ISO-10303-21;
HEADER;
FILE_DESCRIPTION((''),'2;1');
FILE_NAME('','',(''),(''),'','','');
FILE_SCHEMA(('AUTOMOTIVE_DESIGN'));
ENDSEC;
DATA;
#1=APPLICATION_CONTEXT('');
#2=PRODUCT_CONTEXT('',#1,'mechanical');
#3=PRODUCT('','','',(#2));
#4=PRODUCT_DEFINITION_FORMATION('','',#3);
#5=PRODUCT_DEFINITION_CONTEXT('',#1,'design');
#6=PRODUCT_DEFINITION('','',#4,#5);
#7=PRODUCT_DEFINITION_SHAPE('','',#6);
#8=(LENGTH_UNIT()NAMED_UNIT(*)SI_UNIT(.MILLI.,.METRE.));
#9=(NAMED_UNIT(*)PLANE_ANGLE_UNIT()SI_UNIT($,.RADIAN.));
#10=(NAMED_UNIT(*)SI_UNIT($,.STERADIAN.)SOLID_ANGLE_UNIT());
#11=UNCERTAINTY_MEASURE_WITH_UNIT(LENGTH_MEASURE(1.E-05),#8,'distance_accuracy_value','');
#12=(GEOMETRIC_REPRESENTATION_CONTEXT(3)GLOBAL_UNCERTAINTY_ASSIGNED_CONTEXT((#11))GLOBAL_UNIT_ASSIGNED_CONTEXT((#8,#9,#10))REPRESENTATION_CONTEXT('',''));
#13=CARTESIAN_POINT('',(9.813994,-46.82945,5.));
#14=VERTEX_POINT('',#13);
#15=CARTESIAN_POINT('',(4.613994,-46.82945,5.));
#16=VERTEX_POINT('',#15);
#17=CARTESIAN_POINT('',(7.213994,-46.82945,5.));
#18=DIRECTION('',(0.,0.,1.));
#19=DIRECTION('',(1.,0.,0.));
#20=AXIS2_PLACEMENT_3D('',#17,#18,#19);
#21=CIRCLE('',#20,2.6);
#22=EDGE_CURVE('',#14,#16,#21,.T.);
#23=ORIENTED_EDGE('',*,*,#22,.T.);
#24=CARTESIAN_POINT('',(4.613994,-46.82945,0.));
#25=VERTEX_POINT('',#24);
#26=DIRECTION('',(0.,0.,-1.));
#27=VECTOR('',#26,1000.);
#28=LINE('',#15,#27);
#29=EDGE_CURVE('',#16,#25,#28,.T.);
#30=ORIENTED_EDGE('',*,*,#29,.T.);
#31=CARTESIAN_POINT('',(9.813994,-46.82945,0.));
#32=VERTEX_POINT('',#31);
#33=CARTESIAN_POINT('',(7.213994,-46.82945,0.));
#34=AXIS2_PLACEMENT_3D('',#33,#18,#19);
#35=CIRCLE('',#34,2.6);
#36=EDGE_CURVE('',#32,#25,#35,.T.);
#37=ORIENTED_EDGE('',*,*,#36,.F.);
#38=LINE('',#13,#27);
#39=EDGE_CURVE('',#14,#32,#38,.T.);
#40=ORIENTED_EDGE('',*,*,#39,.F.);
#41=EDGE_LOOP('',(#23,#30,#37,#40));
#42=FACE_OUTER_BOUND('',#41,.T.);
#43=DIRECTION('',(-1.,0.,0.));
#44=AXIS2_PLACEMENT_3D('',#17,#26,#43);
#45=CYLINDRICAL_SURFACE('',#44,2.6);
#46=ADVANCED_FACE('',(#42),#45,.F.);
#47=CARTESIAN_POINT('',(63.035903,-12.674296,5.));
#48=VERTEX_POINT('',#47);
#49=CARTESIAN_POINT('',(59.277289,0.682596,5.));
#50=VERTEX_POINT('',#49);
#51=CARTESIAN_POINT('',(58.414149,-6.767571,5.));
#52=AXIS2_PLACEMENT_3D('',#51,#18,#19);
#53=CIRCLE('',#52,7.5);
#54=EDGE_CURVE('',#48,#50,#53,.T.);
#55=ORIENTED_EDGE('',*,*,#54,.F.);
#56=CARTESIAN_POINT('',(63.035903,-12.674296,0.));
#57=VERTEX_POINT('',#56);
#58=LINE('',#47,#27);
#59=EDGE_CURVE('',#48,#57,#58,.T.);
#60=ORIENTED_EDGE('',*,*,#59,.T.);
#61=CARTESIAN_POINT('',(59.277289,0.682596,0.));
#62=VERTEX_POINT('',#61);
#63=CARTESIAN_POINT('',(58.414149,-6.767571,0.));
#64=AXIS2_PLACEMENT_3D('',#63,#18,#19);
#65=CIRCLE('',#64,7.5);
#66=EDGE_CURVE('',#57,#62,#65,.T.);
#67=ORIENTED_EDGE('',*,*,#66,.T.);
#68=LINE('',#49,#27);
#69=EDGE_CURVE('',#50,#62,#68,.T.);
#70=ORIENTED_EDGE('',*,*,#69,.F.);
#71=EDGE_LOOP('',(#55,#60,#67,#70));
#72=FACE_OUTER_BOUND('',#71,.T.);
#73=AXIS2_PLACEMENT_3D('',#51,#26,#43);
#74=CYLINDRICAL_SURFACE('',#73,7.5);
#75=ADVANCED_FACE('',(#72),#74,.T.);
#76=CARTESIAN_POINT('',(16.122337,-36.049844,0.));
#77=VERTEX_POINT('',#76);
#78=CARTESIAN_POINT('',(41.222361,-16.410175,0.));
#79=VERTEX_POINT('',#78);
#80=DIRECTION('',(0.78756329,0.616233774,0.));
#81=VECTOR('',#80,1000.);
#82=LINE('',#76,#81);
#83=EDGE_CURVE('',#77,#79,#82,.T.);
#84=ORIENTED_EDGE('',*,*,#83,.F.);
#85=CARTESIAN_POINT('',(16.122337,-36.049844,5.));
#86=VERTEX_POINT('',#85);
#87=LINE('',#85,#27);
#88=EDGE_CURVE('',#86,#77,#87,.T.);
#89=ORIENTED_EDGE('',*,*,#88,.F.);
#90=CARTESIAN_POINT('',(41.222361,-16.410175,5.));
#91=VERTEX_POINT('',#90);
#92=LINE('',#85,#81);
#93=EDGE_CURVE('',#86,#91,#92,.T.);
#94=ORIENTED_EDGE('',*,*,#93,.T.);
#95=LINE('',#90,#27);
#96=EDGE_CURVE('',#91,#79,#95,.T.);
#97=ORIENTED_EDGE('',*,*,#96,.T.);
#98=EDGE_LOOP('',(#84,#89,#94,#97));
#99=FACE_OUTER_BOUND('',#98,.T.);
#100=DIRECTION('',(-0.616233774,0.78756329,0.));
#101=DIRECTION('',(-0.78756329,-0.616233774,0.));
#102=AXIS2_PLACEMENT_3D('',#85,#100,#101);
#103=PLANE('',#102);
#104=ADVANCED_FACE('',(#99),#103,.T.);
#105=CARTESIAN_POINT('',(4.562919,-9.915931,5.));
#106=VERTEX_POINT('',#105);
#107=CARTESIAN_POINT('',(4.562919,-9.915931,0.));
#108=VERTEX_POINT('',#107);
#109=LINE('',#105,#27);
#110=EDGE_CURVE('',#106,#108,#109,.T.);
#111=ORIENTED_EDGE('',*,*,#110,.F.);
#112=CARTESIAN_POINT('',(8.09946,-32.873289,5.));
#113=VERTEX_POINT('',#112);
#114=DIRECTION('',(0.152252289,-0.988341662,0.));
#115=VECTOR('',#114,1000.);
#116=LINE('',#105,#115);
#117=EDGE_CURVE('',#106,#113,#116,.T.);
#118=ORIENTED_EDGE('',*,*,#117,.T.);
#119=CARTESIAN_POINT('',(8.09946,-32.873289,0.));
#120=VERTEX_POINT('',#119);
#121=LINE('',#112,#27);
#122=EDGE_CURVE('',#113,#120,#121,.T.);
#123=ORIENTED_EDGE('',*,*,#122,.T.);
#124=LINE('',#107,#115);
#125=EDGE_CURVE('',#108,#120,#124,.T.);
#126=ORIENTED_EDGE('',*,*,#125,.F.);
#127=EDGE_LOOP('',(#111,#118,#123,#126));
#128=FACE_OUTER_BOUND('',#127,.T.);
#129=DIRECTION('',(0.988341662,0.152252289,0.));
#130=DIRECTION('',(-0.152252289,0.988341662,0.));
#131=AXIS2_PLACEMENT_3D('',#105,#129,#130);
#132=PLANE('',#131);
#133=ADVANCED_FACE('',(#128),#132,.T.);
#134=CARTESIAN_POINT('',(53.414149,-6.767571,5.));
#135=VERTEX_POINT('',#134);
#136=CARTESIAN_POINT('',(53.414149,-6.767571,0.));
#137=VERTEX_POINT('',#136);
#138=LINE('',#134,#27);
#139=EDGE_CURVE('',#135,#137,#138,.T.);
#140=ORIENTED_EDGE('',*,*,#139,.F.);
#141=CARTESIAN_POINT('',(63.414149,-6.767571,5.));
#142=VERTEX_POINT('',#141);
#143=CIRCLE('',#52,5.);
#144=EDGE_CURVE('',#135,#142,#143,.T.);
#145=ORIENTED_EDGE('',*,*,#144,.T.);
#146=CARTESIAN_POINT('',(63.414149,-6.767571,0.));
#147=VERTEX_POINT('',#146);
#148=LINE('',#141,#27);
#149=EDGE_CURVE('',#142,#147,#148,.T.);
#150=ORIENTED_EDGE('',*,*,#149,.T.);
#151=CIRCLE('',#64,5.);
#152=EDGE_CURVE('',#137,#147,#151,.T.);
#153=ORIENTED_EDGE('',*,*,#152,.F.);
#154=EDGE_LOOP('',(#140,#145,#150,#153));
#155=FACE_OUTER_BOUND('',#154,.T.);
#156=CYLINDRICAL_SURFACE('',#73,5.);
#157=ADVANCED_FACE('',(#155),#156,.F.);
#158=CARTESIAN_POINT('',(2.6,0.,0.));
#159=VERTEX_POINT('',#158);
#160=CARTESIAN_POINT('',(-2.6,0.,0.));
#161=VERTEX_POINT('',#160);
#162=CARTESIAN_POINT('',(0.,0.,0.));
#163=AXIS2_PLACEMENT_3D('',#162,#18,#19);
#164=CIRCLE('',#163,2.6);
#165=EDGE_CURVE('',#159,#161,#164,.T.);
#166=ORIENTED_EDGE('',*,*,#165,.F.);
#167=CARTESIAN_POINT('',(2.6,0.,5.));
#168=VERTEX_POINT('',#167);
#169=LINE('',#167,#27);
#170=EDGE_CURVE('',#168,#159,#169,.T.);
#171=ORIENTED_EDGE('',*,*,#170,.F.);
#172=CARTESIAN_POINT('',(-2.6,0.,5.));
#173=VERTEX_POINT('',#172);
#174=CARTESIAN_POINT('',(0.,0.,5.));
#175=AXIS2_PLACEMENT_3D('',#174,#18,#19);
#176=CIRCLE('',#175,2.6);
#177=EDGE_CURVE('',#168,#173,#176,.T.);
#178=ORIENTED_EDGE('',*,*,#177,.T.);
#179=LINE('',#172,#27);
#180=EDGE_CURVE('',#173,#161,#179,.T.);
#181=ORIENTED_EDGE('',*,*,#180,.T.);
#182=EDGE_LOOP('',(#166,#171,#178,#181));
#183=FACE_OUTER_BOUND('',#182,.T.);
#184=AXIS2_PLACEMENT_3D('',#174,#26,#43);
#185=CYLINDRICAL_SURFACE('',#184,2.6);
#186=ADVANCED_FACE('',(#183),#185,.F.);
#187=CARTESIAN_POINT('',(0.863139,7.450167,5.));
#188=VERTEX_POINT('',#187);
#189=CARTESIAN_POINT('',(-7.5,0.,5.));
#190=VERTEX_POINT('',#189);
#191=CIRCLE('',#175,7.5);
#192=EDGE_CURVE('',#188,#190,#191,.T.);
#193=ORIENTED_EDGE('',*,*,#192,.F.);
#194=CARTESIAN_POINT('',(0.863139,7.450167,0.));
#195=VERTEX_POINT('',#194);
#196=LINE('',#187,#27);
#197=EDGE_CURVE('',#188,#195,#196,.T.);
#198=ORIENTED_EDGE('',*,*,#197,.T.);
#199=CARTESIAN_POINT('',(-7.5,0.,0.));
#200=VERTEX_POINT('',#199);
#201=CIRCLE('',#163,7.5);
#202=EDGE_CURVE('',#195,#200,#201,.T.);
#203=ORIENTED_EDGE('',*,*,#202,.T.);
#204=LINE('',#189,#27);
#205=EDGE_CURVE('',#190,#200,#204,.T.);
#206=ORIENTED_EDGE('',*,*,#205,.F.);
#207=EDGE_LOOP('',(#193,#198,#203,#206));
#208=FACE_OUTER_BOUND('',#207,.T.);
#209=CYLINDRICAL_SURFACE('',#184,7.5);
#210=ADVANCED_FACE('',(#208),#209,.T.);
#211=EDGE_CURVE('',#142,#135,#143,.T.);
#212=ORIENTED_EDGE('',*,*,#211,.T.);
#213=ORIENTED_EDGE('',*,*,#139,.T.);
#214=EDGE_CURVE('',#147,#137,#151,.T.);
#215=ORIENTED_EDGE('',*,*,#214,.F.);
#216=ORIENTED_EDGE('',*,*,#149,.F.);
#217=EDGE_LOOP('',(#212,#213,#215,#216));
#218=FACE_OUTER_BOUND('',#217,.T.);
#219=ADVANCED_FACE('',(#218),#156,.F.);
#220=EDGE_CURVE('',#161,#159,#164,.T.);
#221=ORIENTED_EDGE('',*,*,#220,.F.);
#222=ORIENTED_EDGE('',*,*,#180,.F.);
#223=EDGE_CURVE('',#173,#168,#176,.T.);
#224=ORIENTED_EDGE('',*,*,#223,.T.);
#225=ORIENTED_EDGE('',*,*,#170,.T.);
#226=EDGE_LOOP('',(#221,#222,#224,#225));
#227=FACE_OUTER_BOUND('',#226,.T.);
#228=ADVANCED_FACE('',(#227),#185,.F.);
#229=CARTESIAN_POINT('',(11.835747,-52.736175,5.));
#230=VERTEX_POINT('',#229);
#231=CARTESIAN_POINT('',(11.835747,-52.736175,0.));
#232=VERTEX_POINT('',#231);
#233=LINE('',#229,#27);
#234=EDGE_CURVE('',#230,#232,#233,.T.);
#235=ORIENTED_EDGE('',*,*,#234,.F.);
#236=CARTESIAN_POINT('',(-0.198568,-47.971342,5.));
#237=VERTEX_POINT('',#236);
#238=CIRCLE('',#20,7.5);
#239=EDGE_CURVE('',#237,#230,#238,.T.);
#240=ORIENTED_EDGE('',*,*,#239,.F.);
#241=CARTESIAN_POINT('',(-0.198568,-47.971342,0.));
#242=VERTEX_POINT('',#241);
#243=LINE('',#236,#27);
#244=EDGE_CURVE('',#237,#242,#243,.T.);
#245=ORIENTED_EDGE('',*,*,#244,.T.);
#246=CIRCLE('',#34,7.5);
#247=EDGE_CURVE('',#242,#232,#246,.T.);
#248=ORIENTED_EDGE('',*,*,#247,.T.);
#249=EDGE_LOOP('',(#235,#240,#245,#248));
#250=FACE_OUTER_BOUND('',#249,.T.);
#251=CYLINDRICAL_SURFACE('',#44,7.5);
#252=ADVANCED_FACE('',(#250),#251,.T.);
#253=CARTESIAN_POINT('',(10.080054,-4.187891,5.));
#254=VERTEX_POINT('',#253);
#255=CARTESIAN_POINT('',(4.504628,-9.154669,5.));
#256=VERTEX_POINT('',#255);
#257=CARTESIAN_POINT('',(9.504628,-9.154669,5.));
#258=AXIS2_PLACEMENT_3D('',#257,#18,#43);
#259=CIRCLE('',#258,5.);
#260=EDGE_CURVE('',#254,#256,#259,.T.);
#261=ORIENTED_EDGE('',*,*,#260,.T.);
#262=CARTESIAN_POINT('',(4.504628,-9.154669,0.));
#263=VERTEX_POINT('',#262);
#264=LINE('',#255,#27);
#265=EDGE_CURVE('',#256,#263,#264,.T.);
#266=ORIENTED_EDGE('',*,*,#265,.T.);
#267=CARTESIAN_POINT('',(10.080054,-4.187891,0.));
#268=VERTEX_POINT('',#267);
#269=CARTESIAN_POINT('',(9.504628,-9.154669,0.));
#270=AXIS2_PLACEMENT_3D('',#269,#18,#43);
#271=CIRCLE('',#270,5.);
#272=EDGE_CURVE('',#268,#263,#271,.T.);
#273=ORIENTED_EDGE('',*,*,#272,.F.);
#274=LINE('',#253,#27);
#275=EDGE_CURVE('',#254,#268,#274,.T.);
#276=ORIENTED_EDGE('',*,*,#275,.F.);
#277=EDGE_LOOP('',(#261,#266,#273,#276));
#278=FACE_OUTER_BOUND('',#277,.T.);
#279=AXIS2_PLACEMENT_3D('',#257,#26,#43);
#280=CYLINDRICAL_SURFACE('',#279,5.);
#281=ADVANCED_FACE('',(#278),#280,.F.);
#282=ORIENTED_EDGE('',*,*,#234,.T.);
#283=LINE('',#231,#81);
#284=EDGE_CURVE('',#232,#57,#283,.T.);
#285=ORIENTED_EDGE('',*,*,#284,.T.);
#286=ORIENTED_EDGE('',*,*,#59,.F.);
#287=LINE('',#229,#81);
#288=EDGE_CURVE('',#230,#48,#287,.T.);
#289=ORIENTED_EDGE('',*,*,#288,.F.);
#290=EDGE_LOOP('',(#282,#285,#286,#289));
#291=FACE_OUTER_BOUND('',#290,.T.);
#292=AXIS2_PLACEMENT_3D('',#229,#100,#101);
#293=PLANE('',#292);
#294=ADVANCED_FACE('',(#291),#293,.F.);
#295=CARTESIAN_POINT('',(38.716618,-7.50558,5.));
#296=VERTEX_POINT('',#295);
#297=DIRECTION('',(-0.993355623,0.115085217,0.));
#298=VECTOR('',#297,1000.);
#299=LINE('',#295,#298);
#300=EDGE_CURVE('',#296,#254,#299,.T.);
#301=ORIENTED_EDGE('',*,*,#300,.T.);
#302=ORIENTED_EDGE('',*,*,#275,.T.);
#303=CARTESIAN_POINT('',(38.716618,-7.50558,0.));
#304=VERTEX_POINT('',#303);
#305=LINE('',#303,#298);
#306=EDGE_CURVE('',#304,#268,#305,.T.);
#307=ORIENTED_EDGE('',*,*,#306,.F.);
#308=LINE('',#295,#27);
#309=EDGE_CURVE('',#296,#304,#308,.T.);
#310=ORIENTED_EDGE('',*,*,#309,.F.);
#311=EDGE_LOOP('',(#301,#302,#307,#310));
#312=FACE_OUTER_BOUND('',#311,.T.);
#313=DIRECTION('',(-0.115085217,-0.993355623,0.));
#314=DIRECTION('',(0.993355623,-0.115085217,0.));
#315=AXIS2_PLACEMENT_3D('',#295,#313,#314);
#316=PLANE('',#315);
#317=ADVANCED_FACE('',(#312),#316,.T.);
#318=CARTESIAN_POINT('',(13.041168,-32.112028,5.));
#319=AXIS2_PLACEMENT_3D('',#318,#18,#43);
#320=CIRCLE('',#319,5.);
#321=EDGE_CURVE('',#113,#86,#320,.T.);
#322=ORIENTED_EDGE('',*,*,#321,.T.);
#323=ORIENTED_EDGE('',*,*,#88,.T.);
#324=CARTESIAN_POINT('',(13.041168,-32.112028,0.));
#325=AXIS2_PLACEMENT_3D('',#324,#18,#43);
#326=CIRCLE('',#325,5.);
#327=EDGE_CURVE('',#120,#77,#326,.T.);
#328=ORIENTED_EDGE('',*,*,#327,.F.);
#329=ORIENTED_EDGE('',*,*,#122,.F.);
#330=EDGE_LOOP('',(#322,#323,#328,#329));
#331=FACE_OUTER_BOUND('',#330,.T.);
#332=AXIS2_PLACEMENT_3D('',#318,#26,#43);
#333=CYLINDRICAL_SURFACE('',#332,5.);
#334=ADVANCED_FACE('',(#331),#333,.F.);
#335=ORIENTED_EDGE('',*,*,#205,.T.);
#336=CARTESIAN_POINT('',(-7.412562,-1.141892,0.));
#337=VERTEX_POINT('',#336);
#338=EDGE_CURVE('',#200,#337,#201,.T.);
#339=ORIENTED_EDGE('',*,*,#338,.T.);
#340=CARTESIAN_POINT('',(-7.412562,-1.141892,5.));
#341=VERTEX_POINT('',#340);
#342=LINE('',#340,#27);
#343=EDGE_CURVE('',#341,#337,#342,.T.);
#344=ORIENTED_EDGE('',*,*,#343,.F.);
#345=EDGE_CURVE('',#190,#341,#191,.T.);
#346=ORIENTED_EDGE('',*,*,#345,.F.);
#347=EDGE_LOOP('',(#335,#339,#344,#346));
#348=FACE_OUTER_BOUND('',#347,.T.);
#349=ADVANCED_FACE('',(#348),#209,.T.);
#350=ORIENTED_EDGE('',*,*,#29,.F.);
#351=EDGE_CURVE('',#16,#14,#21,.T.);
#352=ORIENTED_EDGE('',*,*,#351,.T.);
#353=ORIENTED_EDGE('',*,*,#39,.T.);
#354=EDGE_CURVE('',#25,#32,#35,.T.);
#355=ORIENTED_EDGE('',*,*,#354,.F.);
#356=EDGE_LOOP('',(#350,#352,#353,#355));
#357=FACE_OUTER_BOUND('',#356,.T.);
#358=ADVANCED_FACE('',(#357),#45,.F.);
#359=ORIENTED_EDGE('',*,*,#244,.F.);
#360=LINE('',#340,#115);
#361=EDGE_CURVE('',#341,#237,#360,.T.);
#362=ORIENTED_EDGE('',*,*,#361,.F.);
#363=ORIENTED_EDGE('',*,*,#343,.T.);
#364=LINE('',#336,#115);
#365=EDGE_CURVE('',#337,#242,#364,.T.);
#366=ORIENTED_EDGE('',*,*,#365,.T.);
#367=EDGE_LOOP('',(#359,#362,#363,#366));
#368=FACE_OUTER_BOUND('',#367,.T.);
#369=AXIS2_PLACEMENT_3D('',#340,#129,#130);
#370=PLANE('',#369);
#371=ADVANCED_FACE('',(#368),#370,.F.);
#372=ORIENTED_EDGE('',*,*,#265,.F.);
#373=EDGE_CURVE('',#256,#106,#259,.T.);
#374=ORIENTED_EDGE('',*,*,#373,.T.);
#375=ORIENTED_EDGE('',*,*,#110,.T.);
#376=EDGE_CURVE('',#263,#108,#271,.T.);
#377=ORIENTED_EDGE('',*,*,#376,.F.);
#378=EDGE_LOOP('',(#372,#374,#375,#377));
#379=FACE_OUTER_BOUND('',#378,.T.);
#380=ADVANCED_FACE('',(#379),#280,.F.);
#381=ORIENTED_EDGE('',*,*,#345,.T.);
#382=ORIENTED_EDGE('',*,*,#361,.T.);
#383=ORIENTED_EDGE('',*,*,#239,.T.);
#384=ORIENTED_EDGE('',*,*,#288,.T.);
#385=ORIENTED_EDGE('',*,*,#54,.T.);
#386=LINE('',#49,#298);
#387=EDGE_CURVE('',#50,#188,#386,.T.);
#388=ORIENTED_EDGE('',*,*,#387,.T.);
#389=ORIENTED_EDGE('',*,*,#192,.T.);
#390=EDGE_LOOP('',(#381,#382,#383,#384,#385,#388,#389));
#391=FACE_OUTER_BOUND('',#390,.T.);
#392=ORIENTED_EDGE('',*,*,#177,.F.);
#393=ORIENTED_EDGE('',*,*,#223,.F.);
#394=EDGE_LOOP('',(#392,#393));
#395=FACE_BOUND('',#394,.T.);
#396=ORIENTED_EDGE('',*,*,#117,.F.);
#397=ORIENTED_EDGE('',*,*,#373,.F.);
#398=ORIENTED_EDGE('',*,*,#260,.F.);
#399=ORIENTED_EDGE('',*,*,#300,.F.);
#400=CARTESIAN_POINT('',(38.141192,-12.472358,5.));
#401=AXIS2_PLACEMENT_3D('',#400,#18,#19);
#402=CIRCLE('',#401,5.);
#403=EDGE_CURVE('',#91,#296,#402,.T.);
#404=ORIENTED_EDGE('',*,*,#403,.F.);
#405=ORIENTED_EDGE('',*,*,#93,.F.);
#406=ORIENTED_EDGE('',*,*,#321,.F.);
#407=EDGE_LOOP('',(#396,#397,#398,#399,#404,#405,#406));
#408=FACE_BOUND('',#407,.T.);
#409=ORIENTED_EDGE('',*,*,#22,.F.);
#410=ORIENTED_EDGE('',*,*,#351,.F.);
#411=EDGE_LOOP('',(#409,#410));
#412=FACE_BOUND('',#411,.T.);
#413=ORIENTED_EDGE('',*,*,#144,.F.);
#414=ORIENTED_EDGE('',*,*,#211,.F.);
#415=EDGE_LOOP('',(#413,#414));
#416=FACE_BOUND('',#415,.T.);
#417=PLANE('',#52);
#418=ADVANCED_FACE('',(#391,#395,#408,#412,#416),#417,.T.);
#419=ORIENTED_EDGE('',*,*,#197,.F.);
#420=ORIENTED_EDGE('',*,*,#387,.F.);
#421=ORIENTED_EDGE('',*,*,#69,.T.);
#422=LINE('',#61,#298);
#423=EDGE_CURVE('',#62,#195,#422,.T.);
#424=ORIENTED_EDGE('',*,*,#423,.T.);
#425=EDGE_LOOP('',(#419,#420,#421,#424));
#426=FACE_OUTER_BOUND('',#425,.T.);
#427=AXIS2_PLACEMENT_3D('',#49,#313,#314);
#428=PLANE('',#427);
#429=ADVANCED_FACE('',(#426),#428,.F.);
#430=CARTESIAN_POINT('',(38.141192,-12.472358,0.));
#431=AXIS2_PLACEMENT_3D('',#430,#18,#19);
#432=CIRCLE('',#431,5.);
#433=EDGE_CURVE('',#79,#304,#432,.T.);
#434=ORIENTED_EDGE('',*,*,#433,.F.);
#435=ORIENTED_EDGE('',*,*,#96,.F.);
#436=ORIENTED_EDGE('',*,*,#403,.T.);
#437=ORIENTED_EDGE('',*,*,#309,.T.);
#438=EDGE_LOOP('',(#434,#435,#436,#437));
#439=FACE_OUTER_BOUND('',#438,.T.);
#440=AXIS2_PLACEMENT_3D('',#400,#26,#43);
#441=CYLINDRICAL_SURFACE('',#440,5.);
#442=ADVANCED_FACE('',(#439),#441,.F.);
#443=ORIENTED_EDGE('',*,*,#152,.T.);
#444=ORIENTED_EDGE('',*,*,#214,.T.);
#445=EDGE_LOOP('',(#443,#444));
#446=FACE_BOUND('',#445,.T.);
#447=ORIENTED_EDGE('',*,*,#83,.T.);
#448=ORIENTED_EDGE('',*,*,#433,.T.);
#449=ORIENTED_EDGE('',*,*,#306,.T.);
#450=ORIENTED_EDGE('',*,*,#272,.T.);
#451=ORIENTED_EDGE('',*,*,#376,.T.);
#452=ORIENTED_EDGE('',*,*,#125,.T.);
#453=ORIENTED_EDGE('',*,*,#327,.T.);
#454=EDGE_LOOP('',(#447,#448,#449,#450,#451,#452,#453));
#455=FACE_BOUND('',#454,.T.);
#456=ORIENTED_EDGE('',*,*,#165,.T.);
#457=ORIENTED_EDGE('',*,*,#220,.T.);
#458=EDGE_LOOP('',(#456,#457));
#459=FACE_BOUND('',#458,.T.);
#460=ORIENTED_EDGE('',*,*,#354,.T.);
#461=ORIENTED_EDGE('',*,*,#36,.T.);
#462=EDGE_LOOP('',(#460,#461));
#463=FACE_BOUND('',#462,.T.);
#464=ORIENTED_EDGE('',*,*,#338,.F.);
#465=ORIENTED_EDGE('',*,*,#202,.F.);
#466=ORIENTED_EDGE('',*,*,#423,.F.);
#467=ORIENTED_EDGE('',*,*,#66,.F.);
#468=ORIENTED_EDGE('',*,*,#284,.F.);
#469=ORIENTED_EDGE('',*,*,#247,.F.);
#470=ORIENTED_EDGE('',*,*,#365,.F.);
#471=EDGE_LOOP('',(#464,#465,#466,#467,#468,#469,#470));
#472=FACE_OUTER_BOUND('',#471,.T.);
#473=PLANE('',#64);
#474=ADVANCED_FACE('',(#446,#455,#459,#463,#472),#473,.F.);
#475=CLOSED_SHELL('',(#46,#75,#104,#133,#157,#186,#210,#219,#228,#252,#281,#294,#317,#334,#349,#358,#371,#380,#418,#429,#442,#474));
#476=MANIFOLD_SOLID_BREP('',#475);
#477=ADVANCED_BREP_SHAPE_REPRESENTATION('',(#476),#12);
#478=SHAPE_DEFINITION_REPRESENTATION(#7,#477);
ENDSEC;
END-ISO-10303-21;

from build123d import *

# Parameters (mm, degrees)
SKETCH1_R           = 5
SKETCH1_R_2         = 2.6
BOSS_EXTRUDE1_DEPTH = 5


with BuildPart() as part:
    # Sketch1 → Boss-Extrude1 (new body)
    with BuildSketch(Plane.XY):
        with BuildLine():
            Line((-7.412562463, -1.141892169), (-0.198568318, -47.971342146))
            ThreePointArc((-0.198568318, -47.971342146), (4.453004984, -53.802751838), (11.835747448, -52.736174654))
            Line((11.835747448, -52.736174654), (63.035902792, -12.674296032))
            ThreePointArc((63.035902792, -12.674296032), (65.633751361, -4.735983598), (59.277288615, 0.682595814))
            Line((59.277288615, 0.682595814), (0.863139126, 7.450167169))
            ThreePointArc((0.863139126, 7.450167169), (-5.401815198, 5.202921542), (-7.412562463, -1.141892169))
        make_face()
        with Locations((58.414149489, -6.767571355)):
            Circle(SKETCH1_R, mode=Mode.SUBTRACT)
        with Locations((7.213994146, -46.829449977)):
            Circle(SKETCH1_R_2, mode=Mode.SUBTRACT)
        Circle(SKETCH1_R_2, mode=Mode.SUBTRACT)
        with BuildLine():
            Line((38.716618419, -7.505580332), (10.080053588, -4.187891081))
            ThreePointArc((10.080053588, -4.187891081), (5.903417372, -5.686054833), (4.562919195, -9.91593064))
            Line((4.562919195, -9.91593064), (8.099459791, -32.873289294))
            ThreePointArc((8.099459791, -32.873289294), (11.200508659, -36.760895756), (16.122336968, -36.049844299))
            Line((16.122336968, -36.049844299), (41.222361204, -16.410174896))
            ThreePointArc((41.222361204, -16.410174896), (42.95426025, -11.117966607), (38.716618419, -7.505580332))
        make_face(mode=Mode.SUBTRACT)
    extrude(amount=BOSS_EXTRUDE1_DEPTH)


solid = part.part
